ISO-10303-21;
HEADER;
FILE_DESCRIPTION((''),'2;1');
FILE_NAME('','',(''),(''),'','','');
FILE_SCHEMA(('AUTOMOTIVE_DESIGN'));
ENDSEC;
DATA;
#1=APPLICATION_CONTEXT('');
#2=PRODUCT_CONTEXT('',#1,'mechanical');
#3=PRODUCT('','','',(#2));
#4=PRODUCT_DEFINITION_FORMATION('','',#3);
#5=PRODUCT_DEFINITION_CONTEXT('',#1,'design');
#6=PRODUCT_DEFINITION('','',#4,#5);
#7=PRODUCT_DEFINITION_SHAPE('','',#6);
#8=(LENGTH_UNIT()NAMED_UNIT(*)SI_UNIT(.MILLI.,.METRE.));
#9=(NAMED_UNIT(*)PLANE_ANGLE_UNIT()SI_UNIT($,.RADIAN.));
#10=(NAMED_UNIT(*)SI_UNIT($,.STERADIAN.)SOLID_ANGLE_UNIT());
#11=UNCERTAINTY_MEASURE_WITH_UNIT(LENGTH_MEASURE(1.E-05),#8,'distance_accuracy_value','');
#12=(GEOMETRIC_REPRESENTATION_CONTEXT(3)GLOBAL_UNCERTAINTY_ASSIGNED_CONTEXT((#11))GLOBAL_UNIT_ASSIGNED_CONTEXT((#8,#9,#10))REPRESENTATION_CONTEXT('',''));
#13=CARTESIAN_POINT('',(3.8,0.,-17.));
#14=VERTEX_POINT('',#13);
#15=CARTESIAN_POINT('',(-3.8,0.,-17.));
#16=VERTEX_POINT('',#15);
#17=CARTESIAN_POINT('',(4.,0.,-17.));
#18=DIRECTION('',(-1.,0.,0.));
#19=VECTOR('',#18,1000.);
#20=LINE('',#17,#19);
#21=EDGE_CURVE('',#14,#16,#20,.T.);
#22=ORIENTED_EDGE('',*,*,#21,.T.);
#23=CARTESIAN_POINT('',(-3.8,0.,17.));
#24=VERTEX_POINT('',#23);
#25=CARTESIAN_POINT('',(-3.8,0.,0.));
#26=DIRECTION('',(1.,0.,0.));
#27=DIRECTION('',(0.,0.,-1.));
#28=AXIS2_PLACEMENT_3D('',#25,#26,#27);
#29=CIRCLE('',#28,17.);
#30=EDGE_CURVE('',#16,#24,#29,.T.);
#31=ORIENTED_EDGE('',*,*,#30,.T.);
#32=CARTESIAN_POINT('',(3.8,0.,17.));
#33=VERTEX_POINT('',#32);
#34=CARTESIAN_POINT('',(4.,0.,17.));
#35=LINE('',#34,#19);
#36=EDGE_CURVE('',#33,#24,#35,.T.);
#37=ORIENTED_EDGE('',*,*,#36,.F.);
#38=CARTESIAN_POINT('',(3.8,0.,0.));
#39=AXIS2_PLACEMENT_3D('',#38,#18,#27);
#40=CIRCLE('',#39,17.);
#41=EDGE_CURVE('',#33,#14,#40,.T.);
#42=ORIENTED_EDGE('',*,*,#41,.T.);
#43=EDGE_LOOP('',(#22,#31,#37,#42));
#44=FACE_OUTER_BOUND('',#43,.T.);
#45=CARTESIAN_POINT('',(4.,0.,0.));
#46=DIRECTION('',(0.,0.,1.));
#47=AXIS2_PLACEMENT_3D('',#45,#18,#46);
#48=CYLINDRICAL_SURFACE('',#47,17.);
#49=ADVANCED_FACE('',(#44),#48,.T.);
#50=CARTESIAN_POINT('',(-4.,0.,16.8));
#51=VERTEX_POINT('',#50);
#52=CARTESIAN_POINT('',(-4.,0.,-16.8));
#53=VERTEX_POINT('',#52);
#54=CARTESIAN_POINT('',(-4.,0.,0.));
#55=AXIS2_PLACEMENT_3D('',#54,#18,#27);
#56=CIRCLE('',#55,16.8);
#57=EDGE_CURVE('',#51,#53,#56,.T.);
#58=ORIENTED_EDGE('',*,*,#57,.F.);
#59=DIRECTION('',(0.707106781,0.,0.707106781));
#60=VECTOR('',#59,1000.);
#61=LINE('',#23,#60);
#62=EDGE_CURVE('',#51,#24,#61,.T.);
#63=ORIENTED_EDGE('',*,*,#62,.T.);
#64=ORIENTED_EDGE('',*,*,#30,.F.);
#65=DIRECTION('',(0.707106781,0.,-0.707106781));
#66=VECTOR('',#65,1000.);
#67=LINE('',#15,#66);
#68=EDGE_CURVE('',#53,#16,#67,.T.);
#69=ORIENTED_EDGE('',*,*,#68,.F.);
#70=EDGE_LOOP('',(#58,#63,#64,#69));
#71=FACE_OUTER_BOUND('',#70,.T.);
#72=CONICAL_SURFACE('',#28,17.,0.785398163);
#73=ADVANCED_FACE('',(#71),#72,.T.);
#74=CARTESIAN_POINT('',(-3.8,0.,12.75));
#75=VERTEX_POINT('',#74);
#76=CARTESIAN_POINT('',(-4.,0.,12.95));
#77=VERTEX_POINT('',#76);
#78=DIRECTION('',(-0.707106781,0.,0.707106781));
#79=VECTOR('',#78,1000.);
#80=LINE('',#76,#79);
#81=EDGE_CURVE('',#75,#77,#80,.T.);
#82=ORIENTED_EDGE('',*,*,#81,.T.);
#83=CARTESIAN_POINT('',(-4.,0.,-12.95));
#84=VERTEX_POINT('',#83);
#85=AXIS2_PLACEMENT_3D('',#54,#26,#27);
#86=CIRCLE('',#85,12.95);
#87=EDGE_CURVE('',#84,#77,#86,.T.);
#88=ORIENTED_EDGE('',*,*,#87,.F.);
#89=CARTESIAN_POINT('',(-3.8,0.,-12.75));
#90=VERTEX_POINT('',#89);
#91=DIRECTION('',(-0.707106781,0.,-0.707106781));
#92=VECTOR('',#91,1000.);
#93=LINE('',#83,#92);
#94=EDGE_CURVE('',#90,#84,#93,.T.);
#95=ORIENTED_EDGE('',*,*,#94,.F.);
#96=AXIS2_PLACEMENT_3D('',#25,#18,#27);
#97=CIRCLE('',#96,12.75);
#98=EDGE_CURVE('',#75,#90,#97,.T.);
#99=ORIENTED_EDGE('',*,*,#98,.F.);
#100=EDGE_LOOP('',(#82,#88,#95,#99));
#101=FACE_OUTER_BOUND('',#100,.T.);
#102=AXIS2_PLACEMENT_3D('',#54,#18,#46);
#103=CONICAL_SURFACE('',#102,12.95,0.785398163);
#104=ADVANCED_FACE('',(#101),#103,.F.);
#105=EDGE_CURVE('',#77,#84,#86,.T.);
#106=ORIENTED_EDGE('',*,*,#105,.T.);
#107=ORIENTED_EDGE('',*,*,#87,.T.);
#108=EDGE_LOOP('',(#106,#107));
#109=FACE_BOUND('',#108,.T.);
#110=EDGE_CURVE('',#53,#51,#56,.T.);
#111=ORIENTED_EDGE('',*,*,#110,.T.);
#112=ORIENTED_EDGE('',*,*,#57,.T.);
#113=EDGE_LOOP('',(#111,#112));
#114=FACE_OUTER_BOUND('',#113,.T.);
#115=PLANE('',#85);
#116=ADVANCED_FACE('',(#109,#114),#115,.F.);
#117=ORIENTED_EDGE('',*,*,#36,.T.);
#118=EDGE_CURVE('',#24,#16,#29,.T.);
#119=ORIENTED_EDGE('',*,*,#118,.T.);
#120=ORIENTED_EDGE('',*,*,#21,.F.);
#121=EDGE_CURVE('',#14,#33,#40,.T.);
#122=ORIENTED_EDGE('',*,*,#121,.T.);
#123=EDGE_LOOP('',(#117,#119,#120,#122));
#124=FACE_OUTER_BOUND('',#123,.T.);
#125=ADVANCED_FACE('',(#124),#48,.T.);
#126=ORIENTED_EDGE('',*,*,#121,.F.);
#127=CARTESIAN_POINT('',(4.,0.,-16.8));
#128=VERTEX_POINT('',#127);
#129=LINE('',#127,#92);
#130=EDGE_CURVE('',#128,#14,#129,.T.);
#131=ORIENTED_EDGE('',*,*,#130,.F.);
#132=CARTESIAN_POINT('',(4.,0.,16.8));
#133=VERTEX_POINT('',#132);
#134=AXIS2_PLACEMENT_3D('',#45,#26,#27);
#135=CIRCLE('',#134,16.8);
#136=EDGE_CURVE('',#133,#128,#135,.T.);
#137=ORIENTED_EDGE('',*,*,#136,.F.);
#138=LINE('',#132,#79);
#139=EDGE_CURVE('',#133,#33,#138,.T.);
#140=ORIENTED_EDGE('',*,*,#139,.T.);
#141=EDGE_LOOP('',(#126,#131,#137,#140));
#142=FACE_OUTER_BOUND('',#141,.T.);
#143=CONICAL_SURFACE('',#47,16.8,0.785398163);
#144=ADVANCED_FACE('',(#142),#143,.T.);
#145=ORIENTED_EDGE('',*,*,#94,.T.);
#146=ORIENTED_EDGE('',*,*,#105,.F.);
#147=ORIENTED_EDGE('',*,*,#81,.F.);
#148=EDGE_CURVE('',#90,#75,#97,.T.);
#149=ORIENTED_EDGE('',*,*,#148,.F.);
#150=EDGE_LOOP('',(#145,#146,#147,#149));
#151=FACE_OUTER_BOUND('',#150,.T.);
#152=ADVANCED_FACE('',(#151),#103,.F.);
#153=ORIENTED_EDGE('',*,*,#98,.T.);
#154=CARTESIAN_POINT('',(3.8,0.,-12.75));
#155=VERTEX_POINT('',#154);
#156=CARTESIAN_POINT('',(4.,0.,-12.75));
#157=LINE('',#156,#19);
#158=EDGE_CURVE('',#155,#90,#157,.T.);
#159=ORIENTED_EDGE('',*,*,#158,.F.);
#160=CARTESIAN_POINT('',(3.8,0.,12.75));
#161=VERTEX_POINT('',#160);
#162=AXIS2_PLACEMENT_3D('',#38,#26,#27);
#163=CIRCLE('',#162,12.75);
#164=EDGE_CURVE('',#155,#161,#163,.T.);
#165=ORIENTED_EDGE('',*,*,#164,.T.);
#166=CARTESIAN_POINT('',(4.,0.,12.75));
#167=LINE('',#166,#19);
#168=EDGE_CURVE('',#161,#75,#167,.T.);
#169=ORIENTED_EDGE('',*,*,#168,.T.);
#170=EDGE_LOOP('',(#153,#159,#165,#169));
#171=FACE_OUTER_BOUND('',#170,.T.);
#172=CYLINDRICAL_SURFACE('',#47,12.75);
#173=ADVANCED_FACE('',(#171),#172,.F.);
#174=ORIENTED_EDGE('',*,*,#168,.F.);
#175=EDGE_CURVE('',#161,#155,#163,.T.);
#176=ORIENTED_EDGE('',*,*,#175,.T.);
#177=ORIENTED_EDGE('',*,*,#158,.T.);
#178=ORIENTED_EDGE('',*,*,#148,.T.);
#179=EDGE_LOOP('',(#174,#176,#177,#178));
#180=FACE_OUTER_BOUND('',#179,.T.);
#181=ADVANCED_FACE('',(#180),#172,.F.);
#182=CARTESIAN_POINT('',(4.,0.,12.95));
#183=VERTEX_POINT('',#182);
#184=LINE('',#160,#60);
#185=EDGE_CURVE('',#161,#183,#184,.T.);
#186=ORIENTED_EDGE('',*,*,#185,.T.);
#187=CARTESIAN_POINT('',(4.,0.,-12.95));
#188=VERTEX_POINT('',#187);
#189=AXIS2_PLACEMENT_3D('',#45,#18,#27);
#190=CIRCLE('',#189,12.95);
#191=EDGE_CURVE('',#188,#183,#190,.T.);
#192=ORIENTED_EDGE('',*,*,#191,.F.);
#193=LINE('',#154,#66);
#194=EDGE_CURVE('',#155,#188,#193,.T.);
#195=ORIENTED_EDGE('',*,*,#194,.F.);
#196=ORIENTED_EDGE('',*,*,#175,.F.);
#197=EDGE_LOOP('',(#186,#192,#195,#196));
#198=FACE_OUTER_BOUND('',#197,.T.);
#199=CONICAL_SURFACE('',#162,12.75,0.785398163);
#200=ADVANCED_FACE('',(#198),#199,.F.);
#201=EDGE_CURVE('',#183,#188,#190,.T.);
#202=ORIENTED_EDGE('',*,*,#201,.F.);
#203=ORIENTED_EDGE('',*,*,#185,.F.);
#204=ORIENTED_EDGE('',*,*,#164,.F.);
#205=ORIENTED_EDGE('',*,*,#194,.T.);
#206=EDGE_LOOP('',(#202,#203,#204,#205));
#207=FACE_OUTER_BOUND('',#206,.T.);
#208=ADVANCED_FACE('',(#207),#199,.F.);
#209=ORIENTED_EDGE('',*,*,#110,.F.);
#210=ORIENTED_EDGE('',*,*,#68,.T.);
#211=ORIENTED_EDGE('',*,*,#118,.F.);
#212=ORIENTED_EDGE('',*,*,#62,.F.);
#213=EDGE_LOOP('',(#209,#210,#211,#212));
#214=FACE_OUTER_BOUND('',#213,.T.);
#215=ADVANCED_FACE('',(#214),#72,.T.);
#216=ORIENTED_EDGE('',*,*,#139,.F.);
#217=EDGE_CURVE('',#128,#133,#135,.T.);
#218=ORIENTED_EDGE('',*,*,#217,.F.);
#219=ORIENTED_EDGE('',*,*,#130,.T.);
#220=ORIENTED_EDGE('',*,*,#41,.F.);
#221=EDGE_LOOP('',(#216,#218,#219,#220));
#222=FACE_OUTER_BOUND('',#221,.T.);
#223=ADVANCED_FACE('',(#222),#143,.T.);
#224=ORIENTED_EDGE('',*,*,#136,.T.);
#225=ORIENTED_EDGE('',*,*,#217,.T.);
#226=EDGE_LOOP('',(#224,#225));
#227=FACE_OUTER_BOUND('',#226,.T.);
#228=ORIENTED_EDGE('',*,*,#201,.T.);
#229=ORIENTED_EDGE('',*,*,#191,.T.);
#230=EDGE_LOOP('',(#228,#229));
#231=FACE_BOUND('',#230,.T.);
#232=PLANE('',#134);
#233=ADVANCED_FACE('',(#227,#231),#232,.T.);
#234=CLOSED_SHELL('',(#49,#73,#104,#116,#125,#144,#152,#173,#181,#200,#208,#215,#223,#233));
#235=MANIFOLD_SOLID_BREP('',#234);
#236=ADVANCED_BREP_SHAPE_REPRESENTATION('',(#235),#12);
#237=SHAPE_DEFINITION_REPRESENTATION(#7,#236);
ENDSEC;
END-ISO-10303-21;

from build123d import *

# Parameters (mm, degrees)
SKETCH1_R           = 17
SKETCH1_R_2         = 12.75
BOSS_EXTRUDE1_DEPTH = 4
CHAMFER1_SIZE       = 0.2


with BuildPart() as part:
    # Sketch1 → Boss-Extrude1 (new, symmetric)
    with BuildSketch(Plane(origin=(0, 0, 0), x_dir=(0, 0, -1), z_dir=(1, 0, 0))):
        Circle(SKETCH1_R)
        Circle(SKETCH1_R_2, mode=Mode.SUBTRACT)
    extrude(amount=BOSS_EXTRUDE1_DEPTH, both=True)

    # Chamfer1
    chamfer1_edges = [part.edges().sort_by_distance(p)[0] for p in [
        (-4, 0, 17),
        (4, 0, 17),
        (-4, 0, 12.75),
        (4, 0, 12.75),
    ]]
    chamfer(chamfer1_edges, length=CHAMFER1_SIZE)


solid = part.part
